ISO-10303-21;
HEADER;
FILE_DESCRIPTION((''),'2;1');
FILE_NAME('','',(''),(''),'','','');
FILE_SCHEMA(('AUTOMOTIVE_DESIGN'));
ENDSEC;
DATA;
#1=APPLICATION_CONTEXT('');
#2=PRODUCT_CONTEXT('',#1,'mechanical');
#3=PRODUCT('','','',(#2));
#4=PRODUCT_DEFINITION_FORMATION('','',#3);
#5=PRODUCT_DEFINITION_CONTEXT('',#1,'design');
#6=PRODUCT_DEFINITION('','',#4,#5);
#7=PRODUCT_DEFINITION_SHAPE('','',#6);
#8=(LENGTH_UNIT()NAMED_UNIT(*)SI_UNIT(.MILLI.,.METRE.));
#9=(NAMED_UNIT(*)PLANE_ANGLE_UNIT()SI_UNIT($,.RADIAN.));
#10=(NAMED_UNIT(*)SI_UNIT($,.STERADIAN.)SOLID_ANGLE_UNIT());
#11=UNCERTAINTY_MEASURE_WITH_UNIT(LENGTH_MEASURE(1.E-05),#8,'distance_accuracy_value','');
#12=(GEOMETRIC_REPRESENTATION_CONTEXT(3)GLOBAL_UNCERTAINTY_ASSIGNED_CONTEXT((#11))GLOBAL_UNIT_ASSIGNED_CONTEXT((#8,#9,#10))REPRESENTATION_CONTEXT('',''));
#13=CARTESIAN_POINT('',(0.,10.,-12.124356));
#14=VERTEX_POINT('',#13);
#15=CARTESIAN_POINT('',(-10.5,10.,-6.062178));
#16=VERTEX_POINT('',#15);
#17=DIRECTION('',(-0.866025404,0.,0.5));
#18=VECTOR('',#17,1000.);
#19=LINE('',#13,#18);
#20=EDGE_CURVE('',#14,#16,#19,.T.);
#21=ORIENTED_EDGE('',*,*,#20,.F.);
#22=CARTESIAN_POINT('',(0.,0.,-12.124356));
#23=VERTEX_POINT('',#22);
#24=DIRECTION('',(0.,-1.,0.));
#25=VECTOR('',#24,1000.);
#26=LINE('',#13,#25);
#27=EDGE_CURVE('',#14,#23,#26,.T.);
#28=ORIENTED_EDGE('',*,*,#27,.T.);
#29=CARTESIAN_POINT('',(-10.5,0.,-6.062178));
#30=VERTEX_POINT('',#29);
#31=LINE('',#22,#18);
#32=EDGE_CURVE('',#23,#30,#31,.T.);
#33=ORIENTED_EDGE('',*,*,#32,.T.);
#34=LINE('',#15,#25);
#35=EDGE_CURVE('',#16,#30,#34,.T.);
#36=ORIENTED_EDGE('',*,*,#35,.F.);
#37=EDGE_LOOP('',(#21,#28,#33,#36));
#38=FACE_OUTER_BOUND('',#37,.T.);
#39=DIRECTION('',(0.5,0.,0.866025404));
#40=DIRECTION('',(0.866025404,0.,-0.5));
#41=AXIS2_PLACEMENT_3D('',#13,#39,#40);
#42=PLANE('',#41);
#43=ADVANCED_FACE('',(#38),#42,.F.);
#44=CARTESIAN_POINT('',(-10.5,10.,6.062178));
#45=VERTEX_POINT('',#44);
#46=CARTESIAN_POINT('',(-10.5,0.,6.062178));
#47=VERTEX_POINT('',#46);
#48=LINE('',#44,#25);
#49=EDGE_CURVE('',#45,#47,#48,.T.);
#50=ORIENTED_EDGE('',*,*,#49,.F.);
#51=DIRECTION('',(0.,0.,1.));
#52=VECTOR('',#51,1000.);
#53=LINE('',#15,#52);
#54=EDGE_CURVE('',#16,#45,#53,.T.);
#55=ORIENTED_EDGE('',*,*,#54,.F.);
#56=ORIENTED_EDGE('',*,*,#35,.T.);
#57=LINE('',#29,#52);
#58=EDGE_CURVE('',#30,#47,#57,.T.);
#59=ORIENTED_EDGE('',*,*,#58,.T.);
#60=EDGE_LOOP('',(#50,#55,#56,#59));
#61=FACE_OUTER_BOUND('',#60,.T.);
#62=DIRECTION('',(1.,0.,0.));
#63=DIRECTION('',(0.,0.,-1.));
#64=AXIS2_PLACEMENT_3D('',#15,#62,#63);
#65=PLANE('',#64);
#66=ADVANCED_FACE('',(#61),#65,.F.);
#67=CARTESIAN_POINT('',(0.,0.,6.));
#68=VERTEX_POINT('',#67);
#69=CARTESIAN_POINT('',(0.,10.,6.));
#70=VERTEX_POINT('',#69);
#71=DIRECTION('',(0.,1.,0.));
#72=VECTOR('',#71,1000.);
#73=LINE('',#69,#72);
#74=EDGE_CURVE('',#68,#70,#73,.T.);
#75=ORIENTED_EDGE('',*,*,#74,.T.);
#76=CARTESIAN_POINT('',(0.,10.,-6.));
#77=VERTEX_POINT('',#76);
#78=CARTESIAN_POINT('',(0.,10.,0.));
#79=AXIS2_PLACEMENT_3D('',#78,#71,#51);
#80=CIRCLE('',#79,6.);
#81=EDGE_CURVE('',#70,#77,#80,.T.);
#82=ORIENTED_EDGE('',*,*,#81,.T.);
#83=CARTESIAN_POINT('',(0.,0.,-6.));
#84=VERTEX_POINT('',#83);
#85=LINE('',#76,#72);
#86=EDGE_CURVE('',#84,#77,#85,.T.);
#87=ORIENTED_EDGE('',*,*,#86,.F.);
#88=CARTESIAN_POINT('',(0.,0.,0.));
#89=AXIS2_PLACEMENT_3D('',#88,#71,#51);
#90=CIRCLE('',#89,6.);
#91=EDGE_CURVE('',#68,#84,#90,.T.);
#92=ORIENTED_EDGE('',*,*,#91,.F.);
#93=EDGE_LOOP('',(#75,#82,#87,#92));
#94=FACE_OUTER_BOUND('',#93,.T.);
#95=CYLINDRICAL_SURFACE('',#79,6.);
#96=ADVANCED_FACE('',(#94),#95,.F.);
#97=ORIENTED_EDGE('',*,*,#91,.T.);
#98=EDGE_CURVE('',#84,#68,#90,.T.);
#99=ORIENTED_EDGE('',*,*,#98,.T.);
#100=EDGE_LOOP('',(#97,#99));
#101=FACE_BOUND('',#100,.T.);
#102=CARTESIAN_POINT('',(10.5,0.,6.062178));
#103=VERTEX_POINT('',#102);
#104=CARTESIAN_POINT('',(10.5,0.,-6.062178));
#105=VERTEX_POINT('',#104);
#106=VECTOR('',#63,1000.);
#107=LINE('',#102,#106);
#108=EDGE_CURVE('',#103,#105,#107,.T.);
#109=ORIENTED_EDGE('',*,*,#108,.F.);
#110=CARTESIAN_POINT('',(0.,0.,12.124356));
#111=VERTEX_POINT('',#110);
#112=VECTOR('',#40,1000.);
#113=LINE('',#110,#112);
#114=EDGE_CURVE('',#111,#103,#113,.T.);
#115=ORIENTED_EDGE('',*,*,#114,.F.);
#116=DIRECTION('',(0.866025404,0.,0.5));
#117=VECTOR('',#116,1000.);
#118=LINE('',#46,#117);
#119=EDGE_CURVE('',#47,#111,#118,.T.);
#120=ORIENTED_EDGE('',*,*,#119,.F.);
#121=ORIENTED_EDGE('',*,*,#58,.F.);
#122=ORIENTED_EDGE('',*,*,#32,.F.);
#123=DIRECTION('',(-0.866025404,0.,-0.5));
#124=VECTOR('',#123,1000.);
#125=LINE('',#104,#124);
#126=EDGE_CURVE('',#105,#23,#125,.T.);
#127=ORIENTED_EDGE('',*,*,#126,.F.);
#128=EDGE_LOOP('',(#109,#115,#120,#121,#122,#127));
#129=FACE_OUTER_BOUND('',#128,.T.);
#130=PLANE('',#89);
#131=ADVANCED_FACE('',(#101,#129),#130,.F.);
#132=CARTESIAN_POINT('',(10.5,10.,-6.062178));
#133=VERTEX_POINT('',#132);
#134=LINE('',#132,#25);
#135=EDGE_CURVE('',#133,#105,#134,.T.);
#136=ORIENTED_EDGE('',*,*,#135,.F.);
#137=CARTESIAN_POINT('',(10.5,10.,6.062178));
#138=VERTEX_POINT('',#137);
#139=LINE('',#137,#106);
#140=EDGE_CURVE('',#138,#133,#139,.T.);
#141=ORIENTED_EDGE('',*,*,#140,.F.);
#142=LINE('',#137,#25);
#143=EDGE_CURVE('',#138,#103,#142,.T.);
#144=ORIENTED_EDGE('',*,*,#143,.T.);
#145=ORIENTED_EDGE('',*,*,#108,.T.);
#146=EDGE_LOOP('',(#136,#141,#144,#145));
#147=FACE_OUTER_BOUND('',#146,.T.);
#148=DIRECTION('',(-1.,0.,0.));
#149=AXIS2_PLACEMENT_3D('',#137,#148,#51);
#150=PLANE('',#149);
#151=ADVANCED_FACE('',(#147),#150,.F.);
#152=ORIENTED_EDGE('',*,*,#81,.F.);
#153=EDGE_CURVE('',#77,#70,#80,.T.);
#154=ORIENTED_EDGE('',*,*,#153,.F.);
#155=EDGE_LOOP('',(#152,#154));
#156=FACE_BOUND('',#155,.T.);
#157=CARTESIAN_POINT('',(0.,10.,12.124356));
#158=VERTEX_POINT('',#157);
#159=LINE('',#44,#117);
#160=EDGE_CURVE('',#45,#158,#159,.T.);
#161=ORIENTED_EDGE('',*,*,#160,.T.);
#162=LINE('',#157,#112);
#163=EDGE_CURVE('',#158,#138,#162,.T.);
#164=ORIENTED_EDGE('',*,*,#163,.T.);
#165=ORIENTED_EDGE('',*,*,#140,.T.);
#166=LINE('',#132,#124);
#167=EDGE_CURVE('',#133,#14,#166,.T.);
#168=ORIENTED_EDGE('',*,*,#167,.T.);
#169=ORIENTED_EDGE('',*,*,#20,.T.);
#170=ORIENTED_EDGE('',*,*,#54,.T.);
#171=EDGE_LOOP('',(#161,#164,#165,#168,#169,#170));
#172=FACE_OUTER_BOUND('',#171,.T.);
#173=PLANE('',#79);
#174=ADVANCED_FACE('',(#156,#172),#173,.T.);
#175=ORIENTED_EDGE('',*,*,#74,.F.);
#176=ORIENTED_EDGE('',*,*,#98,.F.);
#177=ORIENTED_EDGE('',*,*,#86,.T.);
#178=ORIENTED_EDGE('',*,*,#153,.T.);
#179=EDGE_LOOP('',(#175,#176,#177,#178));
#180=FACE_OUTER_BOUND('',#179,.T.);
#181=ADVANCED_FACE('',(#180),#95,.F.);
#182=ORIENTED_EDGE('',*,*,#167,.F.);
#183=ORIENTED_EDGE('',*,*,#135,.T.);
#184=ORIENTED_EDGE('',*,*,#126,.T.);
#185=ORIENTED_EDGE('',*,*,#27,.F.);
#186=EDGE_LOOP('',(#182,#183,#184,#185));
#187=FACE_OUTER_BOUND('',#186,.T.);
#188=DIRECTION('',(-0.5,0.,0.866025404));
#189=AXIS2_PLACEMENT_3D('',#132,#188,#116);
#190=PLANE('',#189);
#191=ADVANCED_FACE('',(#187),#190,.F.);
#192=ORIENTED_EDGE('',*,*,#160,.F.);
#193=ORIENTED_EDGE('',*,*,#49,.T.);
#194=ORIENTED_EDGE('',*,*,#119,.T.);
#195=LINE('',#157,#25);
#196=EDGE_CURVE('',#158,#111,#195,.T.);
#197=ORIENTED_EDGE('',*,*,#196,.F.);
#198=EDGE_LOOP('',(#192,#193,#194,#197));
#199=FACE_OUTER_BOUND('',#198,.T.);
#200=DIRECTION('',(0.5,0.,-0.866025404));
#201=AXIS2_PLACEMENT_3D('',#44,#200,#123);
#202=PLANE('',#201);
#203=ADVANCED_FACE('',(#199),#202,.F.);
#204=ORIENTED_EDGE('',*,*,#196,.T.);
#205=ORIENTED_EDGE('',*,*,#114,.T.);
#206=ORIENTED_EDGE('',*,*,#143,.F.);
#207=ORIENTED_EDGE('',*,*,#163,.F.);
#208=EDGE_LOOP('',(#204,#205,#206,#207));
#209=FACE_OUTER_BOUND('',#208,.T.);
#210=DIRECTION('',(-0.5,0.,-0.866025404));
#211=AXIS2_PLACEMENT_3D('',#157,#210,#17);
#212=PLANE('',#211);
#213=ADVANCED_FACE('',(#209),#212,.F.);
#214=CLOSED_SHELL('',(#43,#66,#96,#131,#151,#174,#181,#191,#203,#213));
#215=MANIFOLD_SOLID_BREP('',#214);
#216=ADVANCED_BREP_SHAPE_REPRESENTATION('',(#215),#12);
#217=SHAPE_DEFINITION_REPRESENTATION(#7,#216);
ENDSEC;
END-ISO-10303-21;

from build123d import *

# Parameters (mm, degrees)
EXTRUDE_1_DEPTH     = 10
HOLE_WIZARD_M14_1_D = 12


with BuildPart() as part:
    # 草图1 → 凸台-拉伸1 (new body)
    with BuildSketch(Plane(origin=(0, 0, 0), x_dir=(1, 0, 0), z_dir=(0, 1, 0))):
        Polygon((0, 12.124355653), (-10.5, 6.062177826), (-10.5, -6.062177826), (0, -12.124355653), (10.5, -6.062177826), (10.5, 6.062177826), align=None)
    extrude(amount=EXTRUDE_1_DEPTH)

    # M14 螺纹孔1 (through all)
    with Locations(Plane(origin=(0, 10, 0), x_dir=(1, 0, 0), z_dir=(0, 1, 0))):
        with Locations((0, 0)):
            Hole(HOLE_WIZARD_M14_1_D / 2)


solid = part.part
